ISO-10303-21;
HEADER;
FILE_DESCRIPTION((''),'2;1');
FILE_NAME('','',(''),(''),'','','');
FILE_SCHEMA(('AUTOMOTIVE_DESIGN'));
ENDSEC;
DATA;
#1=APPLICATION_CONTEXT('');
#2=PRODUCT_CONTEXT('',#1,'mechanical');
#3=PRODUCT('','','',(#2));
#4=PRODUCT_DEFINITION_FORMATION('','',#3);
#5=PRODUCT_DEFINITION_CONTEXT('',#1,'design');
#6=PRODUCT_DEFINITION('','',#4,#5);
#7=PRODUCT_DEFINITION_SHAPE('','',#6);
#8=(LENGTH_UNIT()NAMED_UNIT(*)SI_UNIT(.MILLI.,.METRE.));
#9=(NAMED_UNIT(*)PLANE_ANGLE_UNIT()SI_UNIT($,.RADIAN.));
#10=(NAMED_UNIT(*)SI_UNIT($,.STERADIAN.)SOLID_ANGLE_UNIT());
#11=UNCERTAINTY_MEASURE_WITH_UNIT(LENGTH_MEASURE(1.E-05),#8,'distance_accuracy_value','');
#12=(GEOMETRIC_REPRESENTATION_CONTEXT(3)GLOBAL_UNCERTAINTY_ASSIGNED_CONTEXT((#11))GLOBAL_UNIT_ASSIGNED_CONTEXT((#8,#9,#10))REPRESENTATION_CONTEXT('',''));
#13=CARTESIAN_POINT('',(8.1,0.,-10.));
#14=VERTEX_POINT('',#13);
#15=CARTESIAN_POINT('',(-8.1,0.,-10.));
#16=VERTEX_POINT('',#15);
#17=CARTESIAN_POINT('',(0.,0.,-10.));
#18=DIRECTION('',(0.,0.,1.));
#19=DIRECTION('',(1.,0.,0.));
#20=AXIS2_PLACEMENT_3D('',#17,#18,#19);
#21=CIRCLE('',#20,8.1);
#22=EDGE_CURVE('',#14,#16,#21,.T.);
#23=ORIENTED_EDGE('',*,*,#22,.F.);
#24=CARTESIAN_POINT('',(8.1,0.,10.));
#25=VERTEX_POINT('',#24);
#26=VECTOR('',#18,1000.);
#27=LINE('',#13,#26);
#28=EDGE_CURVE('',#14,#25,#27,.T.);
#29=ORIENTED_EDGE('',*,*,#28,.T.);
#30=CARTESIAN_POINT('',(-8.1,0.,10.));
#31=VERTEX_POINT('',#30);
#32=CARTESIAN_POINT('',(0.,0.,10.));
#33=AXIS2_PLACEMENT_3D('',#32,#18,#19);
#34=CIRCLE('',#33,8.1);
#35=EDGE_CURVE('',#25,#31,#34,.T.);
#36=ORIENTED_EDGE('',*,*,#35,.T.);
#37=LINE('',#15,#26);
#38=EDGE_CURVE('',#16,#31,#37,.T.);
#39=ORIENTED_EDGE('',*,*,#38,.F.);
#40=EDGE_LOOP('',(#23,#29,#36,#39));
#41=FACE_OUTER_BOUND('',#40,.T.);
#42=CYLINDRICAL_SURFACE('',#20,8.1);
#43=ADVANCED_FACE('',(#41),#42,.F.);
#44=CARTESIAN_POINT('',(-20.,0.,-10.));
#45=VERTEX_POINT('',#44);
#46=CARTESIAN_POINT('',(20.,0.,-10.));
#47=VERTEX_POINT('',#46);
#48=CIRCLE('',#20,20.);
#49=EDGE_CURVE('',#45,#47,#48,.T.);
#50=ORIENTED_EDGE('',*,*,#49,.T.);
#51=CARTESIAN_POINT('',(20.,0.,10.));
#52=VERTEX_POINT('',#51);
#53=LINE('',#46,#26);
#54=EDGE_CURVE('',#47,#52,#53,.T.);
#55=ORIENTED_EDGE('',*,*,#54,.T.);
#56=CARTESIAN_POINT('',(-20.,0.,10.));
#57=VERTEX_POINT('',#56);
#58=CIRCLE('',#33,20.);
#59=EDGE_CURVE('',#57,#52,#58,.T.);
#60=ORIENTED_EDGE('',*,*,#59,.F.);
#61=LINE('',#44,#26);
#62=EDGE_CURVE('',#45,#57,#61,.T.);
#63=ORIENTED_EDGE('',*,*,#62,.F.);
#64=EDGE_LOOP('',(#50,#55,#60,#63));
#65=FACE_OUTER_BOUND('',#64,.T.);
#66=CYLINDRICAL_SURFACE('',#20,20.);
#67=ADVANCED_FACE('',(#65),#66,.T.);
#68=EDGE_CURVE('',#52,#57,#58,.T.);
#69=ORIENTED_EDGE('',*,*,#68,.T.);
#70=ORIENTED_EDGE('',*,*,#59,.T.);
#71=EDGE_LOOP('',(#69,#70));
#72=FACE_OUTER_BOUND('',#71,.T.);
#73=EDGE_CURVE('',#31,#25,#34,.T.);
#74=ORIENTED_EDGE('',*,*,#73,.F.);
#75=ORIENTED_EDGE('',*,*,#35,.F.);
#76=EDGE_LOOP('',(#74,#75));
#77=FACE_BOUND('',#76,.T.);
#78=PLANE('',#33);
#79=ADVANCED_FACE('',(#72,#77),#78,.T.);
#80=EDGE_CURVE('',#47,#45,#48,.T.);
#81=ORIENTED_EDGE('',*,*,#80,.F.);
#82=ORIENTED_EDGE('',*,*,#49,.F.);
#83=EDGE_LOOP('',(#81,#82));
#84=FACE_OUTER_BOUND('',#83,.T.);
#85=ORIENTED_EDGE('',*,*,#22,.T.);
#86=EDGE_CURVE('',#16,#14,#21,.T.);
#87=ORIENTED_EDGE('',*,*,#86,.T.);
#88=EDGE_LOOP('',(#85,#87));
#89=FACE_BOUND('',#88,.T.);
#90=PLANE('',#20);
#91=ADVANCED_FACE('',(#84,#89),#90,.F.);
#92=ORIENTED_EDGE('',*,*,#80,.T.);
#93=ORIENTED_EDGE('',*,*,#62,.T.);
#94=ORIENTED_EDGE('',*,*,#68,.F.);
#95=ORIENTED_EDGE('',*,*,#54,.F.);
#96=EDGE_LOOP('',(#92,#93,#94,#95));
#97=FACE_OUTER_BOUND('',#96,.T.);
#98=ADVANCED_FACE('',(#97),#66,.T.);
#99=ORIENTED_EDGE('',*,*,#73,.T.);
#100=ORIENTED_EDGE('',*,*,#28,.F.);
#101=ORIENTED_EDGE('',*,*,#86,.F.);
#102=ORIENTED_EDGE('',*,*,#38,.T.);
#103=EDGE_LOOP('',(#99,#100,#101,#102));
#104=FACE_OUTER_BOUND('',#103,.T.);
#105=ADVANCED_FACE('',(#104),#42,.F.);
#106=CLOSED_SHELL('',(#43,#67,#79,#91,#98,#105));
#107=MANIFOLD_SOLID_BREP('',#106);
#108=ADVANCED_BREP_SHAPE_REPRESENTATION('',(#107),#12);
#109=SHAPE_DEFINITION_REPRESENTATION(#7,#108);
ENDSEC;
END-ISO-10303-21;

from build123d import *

# Parameters (mm, degrees)
SKETCH_1_R      = 20
SKETCH_1_R_2    = 8.1
EXTRUDE_1_DEPTH = 10


with BuildPart() as part:
    # 草图1 → 凸台-拉伸1 (new, symmetric)
    with BuildSketch(Plane.XY):
        Circle(SKETCH_1_R)
        Circle(SKETCH_1_R_2, mode=Mode.SUBTRACT)
    extrude(amount=EXTRUDE_1_DEPTH, both=True)


solid = part.part
